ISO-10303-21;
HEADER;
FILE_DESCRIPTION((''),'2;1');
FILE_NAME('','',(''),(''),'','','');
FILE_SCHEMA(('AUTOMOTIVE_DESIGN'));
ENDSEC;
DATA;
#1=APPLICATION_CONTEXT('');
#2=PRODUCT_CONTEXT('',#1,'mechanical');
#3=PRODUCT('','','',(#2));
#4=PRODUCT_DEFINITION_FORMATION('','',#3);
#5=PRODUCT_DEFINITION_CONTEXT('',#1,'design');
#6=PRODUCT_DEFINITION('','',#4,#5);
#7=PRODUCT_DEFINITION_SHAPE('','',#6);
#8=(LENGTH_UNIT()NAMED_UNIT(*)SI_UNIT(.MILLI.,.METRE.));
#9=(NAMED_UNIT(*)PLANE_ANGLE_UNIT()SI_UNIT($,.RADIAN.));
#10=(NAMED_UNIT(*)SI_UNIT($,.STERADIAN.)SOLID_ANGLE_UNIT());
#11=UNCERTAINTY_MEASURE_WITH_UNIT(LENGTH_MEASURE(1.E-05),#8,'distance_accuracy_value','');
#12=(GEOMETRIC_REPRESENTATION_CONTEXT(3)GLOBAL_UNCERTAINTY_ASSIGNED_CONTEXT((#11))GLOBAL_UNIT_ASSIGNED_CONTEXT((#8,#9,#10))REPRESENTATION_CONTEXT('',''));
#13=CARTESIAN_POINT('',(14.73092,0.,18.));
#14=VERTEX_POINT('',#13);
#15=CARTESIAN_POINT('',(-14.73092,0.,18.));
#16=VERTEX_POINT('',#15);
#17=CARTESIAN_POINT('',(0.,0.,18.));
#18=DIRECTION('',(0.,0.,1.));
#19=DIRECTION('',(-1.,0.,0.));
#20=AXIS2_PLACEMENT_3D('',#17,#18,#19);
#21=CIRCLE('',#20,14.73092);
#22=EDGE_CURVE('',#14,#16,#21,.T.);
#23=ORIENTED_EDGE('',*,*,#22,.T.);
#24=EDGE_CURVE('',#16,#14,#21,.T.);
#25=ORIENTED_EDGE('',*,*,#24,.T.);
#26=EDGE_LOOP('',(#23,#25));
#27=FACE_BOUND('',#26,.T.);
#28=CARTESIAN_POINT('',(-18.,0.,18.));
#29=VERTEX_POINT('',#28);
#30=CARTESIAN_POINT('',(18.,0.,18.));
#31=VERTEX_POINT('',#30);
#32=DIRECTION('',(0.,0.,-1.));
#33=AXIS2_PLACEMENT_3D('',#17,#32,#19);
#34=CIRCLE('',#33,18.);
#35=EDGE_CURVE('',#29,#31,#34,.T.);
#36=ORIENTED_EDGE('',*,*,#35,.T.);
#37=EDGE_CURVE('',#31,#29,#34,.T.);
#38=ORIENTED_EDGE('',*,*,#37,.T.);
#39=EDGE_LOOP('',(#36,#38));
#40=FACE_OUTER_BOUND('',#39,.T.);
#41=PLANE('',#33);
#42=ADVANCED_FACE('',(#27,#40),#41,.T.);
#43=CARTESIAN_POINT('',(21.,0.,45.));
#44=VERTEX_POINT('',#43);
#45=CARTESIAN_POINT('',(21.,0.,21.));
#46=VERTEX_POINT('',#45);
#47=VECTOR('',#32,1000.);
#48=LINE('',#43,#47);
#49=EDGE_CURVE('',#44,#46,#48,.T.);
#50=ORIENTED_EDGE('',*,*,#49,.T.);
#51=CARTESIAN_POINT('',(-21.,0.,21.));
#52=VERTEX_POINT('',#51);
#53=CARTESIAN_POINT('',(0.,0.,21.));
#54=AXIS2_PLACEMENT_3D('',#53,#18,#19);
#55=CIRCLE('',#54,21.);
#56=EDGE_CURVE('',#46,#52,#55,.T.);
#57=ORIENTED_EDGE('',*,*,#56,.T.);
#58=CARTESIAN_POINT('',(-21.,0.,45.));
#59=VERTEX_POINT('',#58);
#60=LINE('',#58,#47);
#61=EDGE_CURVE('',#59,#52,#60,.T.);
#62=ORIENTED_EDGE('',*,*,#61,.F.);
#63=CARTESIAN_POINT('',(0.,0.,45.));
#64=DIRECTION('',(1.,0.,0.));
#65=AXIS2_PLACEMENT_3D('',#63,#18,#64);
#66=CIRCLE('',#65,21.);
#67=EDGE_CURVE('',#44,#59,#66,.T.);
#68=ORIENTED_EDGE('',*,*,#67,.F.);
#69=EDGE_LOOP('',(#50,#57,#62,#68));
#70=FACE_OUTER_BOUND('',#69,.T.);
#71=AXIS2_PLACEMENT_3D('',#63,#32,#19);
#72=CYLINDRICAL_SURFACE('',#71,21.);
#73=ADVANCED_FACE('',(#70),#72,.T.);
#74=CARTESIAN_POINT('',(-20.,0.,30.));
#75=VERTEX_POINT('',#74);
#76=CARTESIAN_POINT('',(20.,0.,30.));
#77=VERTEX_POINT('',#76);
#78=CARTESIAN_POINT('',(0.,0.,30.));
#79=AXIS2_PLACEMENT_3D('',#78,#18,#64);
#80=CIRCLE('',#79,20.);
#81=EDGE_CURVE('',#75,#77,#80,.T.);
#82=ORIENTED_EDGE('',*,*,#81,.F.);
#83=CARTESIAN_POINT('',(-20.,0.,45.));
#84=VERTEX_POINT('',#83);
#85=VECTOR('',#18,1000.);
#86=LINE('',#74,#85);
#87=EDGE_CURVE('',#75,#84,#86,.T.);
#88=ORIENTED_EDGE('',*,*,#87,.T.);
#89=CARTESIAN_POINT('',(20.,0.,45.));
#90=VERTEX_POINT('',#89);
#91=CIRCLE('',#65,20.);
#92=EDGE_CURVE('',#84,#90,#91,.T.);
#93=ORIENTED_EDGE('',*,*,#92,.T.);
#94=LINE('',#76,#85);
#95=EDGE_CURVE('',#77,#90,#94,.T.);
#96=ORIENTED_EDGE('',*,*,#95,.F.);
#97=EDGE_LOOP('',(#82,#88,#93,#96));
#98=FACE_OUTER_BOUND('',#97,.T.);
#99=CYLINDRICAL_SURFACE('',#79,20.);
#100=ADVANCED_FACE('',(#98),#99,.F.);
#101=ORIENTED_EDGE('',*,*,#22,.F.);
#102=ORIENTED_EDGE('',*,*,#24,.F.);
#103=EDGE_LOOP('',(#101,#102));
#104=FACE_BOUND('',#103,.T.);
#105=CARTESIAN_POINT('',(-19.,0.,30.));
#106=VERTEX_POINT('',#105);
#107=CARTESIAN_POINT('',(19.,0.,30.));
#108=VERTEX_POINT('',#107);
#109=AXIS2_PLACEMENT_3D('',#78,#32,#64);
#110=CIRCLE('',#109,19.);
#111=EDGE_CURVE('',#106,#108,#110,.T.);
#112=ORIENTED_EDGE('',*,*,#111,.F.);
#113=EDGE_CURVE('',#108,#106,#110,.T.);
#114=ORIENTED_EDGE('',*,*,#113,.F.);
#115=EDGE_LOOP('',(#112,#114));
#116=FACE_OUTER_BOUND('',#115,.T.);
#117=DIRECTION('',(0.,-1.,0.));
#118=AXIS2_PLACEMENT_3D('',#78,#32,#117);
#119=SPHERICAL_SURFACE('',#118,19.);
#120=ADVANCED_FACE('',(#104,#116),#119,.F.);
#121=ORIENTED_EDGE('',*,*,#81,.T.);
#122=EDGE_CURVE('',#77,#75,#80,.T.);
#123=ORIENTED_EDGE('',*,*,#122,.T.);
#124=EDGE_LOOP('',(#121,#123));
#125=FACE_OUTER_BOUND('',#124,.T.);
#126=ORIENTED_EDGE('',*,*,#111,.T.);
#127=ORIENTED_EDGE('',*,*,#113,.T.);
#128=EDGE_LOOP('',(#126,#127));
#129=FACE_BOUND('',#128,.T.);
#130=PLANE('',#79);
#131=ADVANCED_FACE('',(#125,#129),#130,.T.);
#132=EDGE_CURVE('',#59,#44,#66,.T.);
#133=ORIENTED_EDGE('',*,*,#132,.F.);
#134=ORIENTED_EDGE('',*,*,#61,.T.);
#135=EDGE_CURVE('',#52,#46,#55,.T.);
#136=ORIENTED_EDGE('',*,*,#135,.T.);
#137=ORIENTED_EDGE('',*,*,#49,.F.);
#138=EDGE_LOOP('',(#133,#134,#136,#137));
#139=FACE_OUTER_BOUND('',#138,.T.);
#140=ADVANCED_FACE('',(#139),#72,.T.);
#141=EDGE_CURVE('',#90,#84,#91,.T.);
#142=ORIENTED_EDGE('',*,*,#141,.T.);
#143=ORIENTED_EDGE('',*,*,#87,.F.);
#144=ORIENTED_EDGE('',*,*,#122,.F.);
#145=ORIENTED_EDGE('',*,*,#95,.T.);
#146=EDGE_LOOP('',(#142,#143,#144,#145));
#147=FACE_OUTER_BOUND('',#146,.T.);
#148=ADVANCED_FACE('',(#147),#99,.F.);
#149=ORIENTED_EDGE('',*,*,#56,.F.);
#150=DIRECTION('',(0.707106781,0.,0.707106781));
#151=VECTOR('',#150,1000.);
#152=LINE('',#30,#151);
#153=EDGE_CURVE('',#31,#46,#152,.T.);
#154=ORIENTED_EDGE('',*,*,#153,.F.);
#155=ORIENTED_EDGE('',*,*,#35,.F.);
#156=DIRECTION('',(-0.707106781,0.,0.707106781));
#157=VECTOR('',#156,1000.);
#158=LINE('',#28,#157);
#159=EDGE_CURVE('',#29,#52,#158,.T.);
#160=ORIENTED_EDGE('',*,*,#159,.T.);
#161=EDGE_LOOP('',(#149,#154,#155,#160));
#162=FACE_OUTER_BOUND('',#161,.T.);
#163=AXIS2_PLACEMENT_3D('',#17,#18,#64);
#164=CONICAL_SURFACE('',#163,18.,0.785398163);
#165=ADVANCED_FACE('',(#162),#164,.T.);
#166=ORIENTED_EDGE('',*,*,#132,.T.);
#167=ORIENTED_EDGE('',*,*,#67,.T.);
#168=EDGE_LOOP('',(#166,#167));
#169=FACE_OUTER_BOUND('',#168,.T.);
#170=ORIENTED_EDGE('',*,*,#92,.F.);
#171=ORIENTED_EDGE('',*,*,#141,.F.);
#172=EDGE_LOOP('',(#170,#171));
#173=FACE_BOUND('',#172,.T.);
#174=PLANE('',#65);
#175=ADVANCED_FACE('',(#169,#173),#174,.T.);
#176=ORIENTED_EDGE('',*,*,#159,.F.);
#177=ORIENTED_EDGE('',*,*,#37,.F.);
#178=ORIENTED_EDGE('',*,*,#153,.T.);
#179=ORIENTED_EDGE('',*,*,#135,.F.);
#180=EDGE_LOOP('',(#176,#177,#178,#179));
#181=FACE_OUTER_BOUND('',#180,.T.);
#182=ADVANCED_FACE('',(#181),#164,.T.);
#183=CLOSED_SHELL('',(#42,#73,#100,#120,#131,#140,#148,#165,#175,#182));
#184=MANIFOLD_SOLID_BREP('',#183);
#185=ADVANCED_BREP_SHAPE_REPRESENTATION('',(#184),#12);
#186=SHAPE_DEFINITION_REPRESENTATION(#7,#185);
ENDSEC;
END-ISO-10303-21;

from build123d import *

# Parameters (mm, degrees)
SKETCH1_R           = 21
BOSS_EXTRUDE1_DEPTH = 45
SKETCH8_R           = 19
CUT_EXTRUDE4_DEPTH  = 15
SKETCH2_R           = 20
CUT_EXTRUDE5_DEPTH  = 15
SKETCH6_R           = 5.5
CUT_EXTRUDE6_DEPTH  = 54.916602267
SKETCH10_R          = 21
CUT_EXTRUDE7_DEPTH  = 10
SKETCH13_R          = 21
CUT_EXTRUDE10_DEPTH = 8
CHAMFER4_SIZE       = 3


with BuildPart() as part:
    # Sketch1 → Boss-Extrude1 (new body)
    with BuildSketch(Plane.XY):
        with Locations(Location((0, 0, 0), (0, 0, 180))):
            Circle(SKETCH1_R)
    extrude(amount=BOSS_EXTRUDE1_DEPTH)

    # Sketch8 → Cut-Extrude4 (cut)
    with BuildSketch(Plane.XY.offset(45)):
        Circle(SKETCH8_R)
    extrude(amount=-CUT_EXTRUDE4_DEPTH, mode=Mode.SUBTRACT)

    # Sketch9 → Cut-Revolve2 (revolve, cut)
    with BuildSketch(Plane.XY.offset(30)):
        with BuildLine():
            Line((19, 0), (-19, 0))
            ThreePointArc((-19, 0), (0, 19), (19, 0))
        make_face()
    revolve(axis=Axis((19, 0, 30), (-1, 0, 0)), mode=Mode.SUBTRACT)

    # Sketch2 → Cut-Extrude5 (cut)
    with BuildSketch(Plane.XY.offset(45)):
        Circle(SKETCH2_R)
    extrude(amount=-CUT_EXTRUDE5_DEPTH, mode=Mode.SUBTRACT)

    # Sketch6 → Cut-Extrude6 (cut, through all)
    with BuildSketch(Plane(origin=(0, 0, 0), x_dir=(-1, 0, 0), z_dir=(0, 0, -1))):
        Circle(SKETCH6_R)
    extrude(amount=-CUT_EXTRUDE6_DEPTH, mode=Mode.SUBTRACT)

    # Sketch10 → Cut-Extrude7 (cut)
    with BuildSketch(Plane(origin=(0, 0, 0), x_dir=(-1, 0, 0), z_dir=(0, 0, -1))):
        Circle(SKETCH10_R)
    extrude(amount=-CUT_EXTRUDE7_DEPTH, mode=Mode.SUBTRACT)

    # Sketch13 → Cut-Extrude10 (cut)
    with BuildSketch(Plane(origin=(0, 0, 10), x_dir=(-1, 0, 0), z_dir=(0, 0, -1))):
        Circle(SKETCH13_R)
    extrude(amount=-CUT_EXTRUDE10_DEPTH, mode=Mode.SUBTRACT)

    # Chamfer4
    chamfer4_edges = [part.edges().sort_by_distance(p)[0] for p in [
        (21, 0, 18),
    ]]
    chamfer(chamfer4_edges, length=CHAMFER4_SIZE)


solid = part.part
